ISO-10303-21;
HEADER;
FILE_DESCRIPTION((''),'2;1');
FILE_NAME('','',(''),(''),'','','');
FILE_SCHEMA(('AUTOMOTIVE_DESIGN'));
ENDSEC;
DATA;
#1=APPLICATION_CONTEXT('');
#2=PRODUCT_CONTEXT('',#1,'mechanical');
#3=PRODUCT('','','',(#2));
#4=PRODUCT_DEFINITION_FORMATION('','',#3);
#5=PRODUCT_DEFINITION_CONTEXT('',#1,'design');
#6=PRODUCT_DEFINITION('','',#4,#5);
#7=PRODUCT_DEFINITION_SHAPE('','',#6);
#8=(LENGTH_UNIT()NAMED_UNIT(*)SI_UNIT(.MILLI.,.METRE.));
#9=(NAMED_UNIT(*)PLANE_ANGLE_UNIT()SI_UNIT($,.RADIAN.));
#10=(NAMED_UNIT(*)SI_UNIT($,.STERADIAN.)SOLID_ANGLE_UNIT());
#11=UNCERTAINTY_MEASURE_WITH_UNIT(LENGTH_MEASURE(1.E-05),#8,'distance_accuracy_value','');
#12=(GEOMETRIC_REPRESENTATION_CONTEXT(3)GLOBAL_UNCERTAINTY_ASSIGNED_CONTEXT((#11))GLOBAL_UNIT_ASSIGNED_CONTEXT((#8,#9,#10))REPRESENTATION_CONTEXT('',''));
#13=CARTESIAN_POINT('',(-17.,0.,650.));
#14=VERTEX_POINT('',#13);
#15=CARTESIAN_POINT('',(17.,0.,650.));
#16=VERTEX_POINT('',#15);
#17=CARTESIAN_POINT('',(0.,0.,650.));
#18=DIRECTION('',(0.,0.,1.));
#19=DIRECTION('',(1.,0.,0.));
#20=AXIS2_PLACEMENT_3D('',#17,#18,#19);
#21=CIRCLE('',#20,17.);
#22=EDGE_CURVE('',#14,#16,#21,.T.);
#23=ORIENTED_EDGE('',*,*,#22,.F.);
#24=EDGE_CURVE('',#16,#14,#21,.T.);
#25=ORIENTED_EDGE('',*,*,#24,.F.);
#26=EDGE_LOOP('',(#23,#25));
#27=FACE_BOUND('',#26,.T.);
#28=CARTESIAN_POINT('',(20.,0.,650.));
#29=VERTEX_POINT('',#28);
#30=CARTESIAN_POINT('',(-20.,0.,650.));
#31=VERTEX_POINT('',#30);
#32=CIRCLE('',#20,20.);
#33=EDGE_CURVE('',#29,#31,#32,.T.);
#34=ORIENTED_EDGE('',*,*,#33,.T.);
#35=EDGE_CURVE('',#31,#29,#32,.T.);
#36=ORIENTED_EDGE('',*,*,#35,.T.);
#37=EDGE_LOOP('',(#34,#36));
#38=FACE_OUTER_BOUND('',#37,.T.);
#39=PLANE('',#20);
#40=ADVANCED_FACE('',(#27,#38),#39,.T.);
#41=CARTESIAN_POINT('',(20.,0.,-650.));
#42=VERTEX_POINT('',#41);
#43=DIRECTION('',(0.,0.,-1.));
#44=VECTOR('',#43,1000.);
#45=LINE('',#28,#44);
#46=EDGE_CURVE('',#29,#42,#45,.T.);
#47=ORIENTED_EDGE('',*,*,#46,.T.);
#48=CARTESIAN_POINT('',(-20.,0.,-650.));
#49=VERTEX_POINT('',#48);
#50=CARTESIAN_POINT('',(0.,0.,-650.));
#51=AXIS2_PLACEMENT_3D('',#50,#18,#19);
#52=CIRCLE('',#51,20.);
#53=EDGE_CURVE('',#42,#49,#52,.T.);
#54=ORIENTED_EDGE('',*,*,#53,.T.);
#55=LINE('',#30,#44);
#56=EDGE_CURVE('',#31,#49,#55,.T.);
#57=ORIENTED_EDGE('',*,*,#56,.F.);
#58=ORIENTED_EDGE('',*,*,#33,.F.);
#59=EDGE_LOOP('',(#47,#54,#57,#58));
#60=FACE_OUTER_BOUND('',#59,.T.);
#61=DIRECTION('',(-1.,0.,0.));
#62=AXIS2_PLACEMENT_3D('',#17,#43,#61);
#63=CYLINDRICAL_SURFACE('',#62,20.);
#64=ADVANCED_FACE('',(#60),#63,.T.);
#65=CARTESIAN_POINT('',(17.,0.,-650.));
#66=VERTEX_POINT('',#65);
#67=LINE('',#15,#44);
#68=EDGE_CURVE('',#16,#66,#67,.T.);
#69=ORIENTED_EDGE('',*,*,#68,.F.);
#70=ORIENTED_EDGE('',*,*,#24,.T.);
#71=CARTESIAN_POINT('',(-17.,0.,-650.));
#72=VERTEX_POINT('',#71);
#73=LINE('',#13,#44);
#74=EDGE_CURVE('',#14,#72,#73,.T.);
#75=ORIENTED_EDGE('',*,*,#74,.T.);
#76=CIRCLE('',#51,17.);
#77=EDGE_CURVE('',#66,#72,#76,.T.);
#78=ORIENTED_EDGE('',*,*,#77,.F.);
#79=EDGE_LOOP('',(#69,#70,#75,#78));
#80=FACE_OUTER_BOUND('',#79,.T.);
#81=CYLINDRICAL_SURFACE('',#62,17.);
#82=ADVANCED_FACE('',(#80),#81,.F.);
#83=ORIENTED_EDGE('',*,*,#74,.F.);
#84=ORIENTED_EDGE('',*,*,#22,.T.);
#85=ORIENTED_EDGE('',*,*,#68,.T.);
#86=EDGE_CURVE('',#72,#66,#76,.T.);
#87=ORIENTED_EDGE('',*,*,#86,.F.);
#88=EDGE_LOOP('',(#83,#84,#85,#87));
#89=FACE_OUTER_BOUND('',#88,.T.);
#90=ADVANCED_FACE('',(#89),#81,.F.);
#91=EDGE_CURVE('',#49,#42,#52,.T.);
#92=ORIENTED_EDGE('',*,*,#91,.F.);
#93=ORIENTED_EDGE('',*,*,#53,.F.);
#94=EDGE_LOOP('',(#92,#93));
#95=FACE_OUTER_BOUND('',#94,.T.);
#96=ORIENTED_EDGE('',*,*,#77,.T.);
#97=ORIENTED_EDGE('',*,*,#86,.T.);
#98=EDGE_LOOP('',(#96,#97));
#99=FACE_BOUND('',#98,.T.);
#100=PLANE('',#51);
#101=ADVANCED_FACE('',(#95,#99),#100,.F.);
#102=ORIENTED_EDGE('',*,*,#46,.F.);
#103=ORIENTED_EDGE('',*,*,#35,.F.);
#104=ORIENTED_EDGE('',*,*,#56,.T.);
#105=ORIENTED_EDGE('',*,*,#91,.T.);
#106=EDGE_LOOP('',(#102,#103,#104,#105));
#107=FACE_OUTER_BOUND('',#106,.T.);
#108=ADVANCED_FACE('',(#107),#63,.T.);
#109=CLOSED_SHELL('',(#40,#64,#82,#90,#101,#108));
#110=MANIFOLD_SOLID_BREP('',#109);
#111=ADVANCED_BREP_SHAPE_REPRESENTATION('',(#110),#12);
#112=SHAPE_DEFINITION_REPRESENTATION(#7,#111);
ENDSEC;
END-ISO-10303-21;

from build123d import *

# Parameters (mm, degrees)
SKETCH1_R           = 20
SKETCH1_R_2         = 17
BOSS_EXTRUDE1_DEPTH = 650


with BuildPart() as part:
    # Sketch1 → Boss-Extrude1 (new, symmetric)
    with BuildSketch(Plane.XY):
        Circle(SKETCH1_R)
        Circle(SKETCH1_R_2, mode=Mode.SUBTRACT)
    extrude(amount=BOSS_EXTRUDE1_DEPTH, both=True)


solid = part.part
